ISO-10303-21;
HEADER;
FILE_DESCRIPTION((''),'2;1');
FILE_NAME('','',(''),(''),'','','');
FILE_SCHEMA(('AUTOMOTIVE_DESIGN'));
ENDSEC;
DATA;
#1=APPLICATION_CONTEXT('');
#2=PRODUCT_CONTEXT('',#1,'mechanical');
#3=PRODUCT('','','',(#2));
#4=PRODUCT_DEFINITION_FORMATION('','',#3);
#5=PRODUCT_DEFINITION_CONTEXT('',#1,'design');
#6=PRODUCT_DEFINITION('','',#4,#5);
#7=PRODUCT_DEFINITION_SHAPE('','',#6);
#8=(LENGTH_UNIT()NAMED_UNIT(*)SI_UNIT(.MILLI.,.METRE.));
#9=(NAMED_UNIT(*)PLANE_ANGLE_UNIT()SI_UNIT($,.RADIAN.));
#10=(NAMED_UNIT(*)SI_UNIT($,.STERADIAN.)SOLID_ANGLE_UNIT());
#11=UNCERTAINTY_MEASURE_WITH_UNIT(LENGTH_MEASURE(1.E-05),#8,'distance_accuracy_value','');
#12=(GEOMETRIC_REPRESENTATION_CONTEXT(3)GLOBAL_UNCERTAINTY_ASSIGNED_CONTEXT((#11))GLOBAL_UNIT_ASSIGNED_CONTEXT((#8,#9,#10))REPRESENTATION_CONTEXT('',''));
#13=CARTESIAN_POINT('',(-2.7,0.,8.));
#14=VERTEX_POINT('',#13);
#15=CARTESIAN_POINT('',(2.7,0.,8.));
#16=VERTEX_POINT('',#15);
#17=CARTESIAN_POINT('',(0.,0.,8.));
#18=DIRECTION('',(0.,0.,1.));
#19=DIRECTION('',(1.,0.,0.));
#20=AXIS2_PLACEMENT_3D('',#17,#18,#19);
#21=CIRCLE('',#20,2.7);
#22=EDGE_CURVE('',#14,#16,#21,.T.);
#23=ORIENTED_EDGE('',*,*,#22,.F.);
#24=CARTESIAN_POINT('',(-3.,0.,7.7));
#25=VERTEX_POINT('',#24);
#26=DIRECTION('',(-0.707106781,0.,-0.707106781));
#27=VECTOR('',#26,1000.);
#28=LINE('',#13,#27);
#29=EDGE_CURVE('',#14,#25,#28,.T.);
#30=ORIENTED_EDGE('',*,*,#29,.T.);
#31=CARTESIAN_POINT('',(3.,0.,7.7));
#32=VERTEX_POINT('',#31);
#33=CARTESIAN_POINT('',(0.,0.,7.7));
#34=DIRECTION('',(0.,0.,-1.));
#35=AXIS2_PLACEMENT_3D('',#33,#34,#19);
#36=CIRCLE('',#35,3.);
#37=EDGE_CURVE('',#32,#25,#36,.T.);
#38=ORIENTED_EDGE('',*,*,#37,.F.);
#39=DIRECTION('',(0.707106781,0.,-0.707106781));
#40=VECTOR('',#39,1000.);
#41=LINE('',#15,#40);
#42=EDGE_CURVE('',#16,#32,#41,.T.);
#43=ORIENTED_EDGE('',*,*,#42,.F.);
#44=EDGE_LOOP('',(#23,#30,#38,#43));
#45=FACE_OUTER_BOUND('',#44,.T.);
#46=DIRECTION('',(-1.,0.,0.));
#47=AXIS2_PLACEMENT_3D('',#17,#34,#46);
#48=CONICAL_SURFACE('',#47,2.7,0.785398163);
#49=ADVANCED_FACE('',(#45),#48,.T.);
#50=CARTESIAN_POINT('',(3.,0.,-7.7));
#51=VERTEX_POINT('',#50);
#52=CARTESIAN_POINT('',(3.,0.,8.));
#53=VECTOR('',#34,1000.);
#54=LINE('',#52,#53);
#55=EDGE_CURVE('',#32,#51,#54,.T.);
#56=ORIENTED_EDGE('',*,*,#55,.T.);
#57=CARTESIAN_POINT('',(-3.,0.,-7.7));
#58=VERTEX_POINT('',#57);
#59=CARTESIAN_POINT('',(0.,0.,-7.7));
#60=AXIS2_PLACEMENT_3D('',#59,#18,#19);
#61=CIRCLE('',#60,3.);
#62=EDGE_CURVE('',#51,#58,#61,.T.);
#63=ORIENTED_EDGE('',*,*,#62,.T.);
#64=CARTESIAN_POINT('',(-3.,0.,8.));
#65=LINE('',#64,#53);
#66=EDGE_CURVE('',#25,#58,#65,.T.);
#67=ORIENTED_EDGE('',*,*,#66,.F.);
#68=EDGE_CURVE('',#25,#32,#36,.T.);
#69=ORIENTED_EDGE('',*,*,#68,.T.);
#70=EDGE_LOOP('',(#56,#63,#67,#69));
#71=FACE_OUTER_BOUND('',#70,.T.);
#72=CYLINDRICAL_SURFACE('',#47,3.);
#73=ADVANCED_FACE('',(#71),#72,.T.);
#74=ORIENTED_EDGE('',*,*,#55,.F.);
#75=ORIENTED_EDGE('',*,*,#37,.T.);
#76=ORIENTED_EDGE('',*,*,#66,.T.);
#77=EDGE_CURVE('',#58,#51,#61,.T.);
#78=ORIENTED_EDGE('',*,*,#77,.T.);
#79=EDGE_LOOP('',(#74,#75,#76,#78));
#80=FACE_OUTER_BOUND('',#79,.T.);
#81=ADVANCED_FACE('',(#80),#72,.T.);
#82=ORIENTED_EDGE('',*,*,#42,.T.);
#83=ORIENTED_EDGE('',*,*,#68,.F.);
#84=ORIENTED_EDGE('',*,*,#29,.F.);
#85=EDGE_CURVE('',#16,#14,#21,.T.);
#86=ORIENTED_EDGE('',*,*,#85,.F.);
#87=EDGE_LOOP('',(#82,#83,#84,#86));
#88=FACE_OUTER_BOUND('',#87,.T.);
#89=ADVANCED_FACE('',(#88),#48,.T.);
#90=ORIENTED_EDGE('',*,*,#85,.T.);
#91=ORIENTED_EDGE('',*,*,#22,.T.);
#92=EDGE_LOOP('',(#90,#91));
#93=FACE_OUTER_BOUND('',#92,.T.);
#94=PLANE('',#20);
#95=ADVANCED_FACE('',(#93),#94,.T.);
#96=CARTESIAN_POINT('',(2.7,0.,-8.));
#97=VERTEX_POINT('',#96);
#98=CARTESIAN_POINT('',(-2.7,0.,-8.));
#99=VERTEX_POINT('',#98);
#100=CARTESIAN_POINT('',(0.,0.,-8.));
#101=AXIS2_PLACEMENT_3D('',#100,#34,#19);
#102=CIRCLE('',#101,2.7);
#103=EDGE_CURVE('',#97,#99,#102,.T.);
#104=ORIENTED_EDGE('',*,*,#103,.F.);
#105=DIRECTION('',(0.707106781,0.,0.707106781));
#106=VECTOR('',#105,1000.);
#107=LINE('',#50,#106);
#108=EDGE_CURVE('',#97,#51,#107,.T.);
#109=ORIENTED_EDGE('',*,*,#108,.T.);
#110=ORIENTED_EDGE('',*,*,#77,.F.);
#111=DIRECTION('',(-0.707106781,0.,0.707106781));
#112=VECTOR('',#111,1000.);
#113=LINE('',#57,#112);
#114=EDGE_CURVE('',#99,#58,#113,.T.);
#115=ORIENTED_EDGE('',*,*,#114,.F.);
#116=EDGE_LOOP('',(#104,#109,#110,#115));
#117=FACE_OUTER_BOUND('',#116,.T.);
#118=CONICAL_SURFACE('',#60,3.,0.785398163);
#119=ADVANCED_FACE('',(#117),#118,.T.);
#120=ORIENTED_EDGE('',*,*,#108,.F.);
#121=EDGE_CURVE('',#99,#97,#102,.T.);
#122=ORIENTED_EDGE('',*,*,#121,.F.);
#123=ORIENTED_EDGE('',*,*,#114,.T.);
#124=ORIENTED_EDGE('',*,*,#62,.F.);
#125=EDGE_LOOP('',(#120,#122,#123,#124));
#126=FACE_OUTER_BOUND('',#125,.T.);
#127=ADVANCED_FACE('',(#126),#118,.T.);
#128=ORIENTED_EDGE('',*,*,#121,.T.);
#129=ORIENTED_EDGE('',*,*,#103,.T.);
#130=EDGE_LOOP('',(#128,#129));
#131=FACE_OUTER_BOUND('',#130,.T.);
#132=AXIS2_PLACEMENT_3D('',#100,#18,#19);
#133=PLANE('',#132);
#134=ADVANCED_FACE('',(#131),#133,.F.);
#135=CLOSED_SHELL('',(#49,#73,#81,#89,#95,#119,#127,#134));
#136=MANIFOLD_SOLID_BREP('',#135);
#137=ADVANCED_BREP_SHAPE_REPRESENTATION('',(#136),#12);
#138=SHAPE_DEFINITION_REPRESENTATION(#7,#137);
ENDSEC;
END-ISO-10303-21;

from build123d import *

# Parameters (mm, degrees)
SKETCH1_R           = 3
BOSS_EXTRUDE1_DEPTH = 8
CHAMFER1_SIZE       = 0.3


with BuildPart() as part:
    # Sketch1 → Boss-Extrude1 (new, symmetric)
    with BuildSketch(Plane.XY):
        Circle(SKETCH1_R)
    extrude(amount=BOSS_EXTRUDE1_DEPTH, both=True)

    # Chamfer1
    chamfer1_edges = [part.edges().sort_by_distance(p)[0] for p in [
        (-3, 0, -8),
        (-3, 0, 8),
    ]]
    chamfer(chamfer1_edges, length=CHAMFER1_SIZE)


solid = part.part
